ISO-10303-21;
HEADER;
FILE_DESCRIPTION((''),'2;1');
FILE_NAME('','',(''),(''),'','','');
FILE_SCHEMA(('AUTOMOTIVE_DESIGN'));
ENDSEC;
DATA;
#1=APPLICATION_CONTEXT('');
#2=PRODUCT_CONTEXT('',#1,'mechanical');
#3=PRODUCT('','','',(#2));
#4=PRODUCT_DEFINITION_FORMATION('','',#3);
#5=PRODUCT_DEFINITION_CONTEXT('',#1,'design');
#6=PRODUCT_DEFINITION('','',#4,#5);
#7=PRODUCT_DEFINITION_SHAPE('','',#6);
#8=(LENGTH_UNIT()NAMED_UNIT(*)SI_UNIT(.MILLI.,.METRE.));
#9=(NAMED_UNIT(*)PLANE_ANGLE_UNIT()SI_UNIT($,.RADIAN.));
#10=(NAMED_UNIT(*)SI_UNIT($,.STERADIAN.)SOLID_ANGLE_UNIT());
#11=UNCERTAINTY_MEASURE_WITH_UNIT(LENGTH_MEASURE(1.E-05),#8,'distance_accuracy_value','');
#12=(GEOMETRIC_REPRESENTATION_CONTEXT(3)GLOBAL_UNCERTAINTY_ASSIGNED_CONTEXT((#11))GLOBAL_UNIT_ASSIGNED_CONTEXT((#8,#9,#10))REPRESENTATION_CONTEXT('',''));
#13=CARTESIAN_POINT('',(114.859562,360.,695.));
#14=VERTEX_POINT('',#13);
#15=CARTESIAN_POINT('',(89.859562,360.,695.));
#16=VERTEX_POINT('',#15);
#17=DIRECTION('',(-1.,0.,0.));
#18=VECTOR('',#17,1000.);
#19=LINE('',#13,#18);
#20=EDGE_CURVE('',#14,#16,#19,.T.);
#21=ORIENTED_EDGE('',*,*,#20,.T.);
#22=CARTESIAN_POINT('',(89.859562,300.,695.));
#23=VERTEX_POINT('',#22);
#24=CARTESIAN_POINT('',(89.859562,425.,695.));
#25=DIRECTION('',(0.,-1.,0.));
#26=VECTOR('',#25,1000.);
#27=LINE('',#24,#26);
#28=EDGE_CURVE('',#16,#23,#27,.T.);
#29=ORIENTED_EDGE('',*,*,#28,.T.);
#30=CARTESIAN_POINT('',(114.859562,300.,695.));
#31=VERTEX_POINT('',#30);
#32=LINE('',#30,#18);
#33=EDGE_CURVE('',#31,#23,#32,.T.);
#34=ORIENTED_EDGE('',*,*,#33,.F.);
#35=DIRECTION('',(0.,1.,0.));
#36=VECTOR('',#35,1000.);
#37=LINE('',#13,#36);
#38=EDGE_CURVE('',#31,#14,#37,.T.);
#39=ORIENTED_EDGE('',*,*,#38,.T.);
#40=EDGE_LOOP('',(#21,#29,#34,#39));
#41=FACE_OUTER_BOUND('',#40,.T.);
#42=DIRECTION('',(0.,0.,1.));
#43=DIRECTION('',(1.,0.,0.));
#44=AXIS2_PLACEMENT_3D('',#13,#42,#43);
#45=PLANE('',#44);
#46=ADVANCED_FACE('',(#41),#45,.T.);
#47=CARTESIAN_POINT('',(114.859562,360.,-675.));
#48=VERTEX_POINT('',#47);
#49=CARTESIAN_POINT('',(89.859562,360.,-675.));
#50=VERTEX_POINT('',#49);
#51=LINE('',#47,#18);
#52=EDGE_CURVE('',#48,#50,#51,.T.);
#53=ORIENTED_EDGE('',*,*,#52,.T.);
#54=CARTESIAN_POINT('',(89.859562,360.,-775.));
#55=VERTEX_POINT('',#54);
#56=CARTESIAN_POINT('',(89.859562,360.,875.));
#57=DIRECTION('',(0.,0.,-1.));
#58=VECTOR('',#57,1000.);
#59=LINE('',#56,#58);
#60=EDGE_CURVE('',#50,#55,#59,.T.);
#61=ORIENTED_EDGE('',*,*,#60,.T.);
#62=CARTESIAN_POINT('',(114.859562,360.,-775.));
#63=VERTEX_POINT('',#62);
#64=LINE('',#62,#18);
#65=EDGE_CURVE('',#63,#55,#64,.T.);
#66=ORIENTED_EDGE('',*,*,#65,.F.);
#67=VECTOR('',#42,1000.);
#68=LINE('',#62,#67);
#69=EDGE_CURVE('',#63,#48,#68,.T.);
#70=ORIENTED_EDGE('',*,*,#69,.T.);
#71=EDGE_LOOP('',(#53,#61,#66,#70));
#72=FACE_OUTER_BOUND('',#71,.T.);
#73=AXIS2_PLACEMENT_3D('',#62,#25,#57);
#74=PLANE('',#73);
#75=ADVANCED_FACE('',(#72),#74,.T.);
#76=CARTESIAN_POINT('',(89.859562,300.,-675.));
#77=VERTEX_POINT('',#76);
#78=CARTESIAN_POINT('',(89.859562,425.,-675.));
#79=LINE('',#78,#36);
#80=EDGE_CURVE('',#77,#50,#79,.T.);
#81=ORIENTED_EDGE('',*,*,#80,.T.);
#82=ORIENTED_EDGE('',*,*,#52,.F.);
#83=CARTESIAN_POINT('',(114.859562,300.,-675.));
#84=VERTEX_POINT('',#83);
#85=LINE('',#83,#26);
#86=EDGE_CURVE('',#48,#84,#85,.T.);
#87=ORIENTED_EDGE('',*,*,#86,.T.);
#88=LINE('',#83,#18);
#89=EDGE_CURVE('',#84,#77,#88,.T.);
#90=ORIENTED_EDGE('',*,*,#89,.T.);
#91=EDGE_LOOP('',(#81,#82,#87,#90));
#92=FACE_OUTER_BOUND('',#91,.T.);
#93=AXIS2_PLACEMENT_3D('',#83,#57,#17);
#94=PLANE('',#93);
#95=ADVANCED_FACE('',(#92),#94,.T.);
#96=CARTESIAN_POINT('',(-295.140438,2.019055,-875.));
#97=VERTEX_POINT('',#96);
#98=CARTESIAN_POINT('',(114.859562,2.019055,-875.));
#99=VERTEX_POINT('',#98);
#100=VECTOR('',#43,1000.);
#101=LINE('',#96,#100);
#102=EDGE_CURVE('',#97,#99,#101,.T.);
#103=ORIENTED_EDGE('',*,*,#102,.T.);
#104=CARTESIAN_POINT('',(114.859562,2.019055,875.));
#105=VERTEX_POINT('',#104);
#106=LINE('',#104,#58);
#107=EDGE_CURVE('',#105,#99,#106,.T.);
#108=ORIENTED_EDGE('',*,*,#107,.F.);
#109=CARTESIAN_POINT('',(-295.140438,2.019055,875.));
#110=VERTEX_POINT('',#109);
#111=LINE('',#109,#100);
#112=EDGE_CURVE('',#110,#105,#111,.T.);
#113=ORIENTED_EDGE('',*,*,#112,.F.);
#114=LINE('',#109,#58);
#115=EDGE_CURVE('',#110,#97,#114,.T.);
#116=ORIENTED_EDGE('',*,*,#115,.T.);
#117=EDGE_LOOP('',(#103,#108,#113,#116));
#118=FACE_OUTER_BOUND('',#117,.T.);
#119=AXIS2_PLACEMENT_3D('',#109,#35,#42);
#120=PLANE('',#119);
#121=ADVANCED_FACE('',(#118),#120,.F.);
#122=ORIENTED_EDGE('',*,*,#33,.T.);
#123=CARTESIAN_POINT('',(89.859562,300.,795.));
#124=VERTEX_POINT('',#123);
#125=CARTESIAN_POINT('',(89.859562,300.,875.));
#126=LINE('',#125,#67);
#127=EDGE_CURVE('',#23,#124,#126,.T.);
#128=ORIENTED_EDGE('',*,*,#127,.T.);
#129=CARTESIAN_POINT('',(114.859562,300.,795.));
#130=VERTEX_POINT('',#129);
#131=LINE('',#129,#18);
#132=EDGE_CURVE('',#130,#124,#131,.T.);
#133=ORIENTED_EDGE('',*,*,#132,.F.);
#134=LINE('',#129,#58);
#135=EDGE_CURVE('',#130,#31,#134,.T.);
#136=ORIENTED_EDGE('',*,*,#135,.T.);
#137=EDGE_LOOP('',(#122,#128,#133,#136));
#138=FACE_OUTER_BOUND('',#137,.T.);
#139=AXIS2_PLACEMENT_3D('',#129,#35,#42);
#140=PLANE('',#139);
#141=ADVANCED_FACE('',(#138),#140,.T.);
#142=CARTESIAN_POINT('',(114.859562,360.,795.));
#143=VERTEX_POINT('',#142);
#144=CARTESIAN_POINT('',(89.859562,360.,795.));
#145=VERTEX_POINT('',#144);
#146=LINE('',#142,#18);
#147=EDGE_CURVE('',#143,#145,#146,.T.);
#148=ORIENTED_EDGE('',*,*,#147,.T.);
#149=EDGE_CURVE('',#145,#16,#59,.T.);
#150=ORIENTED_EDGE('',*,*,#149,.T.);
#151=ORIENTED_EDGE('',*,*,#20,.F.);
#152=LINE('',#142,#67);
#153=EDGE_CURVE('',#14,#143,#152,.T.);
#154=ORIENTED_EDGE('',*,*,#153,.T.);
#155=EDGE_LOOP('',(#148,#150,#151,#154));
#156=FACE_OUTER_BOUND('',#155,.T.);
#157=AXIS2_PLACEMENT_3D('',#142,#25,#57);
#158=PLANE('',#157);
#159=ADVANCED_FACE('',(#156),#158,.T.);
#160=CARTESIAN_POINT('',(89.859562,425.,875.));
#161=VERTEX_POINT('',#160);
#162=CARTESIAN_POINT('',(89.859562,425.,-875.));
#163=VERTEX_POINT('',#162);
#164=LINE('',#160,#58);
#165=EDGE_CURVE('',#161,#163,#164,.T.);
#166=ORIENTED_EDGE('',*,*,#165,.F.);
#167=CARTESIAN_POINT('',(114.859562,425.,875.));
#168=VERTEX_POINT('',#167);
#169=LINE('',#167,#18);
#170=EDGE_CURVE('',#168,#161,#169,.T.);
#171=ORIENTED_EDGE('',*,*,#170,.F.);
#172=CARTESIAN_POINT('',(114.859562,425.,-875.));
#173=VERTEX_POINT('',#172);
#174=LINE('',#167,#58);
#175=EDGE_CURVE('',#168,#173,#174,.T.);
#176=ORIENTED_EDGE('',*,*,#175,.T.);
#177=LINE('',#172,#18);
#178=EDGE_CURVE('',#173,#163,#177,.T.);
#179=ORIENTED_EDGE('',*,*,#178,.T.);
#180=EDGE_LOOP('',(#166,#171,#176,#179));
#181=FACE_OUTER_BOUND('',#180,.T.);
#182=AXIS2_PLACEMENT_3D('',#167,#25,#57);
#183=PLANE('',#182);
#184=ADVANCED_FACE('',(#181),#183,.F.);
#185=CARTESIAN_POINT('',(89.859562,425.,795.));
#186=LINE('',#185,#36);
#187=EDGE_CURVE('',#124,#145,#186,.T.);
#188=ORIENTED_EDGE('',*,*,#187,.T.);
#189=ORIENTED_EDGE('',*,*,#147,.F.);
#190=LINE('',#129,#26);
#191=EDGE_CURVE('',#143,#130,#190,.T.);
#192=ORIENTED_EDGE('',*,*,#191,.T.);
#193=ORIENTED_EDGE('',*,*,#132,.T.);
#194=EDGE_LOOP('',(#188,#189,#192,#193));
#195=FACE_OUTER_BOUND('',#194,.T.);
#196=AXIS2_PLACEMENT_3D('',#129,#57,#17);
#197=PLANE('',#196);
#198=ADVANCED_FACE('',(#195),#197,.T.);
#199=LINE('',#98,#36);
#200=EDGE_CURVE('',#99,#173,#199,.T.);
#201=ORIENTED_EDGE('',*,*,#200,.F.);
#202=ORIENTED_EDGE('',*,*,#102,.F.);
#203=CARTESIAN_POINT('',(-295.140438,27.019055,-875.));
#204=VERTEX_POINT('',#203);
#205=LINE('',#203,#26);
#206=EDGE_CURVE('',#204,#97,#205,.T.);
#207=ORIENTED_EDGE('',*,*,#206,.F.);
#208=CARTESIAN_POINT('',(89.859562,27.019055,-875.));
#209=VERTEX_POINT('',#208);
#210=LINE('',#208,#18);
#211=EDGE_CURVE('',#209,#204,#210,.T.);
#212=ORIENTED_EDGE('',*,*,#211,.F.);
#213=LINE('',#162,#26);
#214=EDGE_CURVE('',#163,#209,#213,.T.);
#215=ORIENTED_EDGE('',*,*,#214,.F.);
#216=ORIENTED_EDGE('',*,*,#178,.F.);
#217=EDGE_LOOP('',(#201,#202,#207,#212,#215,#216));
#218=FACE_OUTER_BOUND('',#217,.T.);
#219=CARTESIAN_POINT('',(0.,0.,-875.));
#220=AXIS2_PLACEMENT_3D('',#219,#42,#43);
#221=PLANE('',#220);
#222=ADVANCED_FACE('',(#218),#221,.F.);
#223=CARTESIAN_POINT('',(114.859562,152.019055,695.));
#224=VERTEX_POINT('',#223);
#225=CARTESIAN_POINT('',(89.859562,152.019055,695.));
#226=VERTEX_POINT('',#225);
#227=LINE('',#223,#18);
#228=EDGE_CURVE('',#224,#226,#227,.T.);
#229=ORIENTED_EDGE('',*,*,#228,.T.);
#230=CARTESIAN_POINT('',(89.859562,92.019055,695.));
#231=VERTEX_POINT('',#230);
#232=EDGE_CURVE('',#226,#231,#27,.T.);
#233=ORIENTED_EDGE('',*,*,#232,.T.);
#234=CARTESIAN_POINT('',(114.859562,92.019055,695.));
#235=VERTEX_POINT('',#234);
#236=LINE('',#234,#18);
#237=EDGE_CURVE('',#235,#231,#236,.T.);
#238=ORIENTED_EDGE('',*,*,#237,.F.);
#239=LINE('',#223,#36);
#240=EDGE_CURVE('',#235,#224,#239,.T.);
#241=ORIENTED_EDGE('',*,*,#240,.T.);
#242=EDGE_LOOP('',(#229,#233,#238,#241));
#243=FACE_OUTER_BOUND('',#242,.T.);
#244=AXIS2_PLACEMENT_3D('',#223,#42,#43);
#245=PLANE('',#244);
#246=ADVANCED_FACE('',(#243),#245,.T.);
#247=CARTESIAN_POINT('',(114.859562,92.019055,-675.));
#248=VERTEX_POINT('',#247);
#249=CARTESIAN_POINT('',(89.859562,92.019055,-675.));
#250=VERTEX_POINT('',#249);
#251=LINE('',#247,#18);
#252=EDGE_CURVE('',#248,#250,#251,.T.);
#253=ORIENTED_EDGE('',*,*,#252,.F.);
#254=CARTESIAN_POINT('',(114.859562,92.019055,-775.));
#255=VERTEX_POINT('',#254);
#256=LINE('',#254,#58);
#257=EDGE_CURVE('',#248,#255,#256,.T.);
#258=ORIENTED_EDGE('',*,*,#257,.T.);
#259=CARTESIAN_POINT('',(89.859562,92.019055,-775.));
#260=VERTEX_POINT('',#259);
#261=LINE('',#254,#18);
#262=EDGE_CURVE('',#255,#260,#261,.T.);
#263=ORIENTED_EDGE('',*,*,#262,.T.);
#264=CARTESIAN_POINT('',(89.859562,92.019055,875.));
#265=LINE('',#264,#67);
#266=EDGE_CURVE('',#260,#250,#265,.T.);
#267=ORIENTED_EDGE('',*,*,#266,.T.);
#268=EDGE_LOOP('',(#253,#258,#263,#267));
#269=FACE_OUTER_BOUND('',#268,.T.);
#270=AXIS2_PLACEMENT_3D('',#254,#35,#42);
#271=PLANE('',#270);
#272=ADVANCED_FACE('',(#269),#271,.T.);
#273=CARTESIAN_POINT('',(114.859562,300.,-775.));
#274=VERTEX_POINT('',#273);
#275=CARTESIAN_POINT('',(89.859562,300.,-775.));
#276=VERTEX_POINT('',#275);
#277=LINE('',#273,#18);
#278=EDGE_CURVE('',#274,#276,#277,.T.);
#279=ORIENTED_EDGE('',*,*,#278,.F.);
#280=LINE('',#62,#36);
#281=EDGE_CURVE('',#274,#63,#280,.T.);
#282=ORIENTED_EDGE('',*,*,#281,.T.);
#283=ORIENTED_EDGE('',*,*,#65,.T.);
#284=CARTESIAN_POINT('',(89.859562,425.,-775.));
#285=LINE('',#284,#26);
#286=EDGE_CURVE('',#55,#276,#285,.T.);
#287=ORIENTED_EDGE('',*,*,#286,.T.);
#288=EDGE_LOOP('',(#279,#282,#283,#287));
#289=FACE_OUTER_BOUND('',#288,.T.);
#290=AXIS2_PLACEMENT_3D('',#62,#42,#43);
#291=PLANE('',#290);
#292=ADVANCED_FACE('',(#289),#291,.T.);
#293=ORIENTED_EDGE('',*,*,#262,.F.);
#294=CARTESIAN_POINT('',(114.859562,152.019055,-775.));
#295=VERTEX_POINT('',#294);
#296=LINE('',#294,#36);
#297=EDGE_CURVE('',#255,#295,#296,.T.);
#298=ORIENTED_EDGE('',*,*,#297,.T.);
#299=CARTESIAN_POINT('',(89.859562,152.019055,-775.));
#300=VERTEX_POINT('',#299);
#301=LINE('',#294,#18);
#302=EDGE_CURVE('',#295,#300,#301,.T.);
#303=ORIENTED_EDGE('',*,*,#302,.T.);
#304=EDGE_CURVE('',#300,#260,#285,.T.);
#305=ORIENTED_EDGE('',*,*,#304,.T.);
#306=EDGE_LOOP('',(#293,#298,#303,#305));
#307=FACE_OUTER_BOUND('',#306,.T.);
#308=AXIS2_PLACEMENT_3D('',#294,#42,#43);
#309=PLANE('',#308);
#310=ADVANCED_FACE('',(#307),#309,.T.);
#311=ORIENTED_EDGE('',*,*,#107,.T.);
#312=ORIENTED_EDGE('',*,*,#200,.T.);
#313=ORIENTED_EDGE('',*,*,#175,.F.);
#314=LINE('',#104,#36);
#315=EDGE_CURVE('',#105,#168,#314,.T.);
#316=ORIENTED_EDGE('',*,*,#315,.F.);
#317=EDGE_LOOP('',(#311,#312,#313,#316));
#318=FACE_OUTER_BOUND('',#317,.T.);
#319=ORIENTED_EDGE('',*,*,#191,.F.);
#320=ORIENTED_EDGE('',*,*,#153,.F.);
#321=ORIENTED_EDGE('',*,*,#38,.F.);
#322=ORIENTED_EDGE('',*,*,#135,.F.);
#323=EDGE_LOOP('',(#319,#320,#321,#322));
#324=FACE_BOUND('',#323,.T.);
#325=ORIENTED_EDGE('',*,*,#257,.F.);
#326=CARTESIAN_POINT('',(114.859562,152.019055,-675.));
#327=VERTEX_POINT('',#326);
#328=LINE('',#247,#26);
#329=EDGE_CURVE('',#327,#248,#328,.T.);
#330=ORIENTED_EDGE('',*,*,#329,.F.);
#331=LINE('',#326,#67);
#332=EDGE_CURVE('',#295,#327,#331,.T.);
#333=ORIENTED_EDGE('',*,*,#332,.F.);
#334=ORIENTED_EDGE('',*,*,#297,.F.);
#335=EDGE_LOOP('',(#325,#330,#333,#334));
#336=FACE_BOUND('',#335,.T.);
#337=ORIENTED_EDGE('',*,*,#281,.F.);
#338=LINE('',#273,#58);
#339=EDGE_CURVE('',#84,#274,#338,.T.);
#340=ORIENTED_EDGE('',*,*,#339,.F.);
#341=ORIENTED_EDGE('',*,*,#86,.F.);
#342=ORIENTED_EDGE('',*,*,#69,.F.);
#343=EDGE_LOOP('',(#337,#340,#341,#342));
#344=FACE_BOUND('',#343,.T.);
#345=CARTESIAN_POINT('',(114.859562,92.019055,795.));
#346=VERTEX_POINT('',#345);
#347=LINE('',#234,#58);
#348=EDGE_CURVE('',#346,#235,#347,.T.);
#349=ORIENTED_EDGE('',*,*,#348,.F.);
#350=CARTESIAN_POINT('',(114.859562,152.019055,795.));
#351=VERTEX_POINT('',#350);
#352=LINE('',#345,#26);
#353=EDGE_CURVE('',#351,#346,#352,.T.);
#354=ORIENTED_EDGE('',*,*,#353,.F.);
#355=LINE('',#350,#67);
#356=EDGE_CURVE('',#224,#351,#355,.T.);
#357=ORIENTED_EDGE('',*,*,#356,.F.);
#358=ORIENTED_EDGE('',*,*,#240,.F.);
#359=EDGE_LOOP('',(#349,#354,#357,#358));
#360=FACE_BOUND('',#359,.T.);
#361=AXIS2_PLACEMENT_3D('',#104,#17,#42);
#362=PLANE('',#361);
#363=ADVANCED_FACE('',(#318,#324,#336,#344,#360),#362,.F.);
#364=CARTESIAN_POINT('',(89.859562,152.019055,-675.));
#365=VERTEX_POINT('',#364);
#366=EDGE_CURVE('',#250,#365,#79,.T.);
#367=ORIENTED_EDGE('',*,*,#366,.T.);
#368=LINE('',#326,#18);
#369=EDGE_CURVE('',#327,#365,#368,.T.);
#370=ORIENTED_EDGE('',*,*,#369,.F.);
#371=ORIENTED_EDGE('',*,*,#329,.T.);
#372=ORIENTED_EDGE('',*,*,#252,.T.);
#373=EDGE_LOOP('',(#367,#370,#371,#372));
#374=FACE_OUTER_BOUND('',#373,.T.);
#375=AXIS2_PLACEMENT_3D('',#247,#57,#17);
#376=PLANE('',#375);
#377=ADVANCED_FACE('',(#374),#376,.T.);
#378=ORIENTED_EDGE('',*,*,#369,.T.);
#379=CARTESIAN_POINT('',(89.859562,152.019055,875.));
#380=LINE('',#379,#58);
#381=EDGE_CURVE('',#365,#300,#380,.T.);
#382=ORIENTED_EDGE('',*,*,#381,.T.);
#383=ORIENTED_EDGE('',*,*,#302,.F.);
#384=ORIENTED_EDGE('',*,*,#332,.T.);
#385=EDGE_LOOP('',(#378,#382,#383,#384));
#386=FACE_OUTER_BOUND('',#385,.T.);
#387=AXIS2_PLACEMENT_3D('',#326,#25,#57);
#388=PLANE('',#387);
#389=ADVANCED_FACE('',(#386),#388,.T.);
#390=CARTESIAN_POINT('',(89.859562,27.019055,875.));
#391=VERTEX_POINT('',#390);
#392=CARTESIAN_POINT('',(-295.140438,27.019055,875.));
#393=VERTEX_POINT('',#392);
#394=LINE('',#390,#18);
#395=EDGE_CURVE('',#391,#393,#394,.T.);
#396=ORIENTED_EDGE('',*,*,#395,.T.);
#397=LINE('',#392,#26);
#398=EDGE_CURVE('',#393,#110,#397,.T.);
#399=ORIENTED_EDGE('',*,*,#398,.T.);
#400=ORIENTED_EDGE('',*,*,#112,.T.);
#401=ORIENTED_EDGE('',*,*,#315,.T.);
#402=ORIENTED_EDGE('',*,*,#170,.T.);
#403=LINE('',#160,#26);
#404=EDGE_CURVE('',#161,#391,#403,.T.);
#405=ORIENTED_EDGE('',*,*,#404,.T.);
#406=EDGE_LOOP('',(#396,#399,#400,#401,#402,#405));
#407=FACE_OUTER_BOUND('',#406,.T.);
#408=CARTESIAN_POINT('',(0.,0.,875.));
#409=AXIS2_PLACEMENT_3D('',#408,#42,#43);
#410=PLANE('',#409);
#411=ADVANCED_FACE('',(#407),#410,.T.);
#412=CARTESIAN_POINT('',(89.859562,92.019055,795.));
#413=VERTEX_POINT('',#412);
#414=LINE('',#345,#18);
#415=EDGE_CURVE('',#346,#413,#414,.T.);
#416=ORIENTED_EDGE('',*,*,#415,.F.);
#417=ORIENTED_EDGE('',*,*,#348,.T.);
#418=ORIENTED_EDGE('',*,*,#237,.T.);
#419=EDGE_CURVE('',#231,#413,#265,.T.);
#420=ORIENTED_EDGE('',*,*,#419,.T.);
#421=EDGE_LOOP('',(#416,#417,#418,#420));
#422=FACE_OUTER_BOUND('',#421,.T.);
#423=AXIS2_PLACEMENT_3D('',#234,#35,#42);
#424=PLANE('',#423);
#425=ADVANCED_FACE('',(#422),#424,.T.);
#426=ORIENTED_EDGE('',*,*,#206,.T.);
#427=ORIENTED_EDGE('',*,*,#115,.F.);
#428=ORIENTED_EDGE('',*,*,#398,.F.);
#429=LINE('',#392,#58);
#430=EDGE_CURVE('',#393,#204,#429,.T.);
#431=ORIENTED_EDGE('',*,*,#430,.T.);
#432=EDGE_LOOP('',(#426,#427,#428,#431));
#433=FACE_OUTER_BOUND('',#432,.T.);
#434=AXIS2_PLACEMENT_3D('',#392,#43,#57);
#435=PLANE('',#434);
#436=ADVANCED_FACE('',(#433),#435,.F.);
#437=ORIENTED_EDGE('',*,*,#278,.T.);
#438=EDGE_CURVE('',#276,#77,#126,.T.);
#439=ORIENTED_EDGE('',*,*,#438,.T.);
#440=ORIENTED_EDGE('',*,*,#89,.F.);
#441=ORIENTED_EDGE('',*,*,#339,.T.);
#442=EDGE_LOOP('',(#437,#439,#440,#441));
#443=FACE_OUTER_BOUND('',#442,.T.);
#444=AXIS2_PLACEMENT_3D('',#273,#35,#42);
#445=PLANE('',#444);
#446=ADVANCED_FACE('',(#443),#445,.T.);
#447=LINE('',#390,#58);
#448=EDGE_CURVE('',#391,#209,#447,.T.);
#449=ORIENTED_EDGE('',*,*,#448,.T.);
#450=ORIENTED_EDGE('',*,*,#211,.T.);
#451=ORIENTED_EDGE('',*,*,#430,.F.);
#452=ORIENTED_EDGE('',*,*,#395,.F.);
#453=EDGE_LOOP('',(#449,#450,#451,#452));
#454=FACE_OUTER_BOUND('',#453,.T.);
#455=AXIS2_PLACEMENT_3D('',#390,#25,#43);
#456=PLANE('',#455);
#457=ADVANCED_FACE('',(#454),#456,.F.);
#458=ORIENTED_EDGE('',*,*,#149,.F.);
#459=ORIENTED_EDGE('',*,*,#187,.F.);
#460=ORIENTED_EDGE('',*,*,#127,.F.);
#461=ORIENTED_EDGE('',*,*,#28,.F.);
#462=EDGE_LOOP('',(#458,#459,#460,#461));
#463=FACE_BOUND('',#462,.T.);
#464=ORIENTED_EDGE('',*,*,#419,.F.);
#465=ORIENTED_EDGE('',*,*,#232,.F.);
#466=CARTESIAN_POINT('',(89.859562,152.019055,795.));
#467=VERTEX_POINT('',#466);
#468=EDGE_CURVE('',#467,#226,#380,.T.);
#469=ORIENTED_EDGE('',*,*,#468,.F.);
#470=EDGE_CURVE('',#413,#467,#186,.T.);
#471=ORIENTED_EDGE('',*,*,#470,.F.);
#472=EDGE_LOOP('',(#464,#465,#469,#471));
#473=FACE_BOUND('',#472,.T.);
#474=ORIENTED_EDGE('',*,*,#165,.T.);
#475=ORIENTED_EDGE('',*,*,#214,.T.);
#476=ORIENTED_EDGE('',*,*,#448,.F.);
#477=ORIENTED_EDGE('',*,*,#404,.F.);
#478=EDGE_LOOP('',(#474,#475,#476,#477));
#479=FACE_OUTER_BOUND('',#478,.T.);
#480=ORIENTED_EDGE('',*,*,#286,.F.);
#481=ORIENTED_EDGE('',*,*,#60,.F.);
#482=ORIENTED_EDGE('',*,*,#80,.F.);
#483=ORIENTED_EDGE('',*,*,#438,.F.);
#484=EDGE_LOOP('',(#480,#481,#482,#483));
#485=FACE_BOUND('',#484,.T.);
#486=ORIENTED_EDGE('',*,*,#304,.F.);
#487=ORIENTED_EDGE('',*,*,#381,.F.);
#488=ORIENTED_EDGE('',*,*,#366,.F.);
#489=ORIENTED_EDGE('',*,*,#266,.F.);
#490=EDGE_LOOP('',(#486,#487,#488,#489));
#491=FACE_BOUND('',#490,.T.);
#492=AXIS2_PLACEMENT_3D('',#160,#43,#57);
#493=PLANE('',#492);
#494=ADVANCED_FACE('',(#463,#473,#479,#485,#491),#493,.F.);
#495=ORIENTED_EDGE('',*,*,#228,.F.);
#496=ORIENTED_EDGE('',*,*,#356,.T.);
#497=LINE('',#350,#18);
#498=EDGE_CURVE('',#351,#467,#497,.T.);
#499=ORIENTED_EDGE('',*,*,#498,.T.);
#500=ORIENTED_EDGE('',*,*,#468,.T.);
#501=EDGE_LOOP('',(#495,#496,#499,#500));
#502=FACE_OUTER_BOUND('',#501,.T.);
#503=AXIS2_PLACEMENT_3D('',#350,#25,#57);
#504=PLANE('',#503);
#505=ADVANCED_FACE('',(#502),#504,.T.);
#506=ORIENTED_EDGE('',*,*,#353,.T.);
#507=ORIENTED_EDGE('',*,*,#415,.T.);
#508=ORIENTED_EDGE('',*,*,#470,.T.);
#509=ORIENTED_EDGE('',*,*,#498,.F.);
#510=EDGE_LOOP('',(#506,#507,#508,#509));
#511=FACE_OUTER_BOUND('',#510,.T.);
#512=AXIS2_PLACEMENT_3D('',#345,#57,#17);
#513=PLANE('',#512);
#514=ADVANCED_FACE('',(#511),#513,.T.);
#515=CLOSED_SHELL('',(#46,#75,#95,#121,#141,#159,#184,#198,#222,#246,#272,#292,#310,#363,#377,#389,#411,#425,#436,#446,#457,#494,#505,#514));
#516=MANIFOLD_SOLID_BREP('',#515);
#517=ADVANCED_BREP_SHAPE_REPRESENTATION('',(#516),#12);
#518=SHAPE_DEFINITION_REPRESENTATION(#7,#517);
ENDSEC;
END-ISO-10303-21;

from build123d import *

# Parameters (mm, degrees)
EXTRUDE_1_DEPTH     = 875
SKETCH_2_W          = 100
SKETCH_2_H          = 60
CUT_EXTRUDE_2_DEPTH = 1017.542118193


with BuildPart() as part:
    # 草图1 → 凸台-拉伸1 (new, symmetric)
    with BuildSketch(Plane.XY):
        Polygon((-295.14043786, 27.019055308), (-295.14043786, 2.019055308), (114.859562138, 2.019055308), (114.859562138, 425), (89.859562138, 425), (89.859562138, 27.019055308), align=None)
    extrude(amount=EXTRUDE_1_DEPTH, both=True)

    # 草图2 → 切除-拉伸2 (cut, through all)
    with BuildSketch(Plane(origin=(0, 0, 0), x_dir=(0, 0, -1), z_dir=(1, 0, 0))):
        with Locations((725, 330)):
            Rectangle(SKETCH_2_W, SKETCH_2_H)
        with Locations((-745, 330)):
            Rectangle(SKETCH_2_W, SKETCH_2_H)
        with Locations((725, 122.019055308)):
            Rectangle(SKETCH_2_W, SKETCH_2_H)
        with Locations((-745, 122.019055308)):
            Rectangle(SKETCH_2_W, SKETCH_2_H)
    extrude(amount=CUT_EXTRUDE_2_DEPTH, mode=Mode.SUBTRACT)


solid = part.part
